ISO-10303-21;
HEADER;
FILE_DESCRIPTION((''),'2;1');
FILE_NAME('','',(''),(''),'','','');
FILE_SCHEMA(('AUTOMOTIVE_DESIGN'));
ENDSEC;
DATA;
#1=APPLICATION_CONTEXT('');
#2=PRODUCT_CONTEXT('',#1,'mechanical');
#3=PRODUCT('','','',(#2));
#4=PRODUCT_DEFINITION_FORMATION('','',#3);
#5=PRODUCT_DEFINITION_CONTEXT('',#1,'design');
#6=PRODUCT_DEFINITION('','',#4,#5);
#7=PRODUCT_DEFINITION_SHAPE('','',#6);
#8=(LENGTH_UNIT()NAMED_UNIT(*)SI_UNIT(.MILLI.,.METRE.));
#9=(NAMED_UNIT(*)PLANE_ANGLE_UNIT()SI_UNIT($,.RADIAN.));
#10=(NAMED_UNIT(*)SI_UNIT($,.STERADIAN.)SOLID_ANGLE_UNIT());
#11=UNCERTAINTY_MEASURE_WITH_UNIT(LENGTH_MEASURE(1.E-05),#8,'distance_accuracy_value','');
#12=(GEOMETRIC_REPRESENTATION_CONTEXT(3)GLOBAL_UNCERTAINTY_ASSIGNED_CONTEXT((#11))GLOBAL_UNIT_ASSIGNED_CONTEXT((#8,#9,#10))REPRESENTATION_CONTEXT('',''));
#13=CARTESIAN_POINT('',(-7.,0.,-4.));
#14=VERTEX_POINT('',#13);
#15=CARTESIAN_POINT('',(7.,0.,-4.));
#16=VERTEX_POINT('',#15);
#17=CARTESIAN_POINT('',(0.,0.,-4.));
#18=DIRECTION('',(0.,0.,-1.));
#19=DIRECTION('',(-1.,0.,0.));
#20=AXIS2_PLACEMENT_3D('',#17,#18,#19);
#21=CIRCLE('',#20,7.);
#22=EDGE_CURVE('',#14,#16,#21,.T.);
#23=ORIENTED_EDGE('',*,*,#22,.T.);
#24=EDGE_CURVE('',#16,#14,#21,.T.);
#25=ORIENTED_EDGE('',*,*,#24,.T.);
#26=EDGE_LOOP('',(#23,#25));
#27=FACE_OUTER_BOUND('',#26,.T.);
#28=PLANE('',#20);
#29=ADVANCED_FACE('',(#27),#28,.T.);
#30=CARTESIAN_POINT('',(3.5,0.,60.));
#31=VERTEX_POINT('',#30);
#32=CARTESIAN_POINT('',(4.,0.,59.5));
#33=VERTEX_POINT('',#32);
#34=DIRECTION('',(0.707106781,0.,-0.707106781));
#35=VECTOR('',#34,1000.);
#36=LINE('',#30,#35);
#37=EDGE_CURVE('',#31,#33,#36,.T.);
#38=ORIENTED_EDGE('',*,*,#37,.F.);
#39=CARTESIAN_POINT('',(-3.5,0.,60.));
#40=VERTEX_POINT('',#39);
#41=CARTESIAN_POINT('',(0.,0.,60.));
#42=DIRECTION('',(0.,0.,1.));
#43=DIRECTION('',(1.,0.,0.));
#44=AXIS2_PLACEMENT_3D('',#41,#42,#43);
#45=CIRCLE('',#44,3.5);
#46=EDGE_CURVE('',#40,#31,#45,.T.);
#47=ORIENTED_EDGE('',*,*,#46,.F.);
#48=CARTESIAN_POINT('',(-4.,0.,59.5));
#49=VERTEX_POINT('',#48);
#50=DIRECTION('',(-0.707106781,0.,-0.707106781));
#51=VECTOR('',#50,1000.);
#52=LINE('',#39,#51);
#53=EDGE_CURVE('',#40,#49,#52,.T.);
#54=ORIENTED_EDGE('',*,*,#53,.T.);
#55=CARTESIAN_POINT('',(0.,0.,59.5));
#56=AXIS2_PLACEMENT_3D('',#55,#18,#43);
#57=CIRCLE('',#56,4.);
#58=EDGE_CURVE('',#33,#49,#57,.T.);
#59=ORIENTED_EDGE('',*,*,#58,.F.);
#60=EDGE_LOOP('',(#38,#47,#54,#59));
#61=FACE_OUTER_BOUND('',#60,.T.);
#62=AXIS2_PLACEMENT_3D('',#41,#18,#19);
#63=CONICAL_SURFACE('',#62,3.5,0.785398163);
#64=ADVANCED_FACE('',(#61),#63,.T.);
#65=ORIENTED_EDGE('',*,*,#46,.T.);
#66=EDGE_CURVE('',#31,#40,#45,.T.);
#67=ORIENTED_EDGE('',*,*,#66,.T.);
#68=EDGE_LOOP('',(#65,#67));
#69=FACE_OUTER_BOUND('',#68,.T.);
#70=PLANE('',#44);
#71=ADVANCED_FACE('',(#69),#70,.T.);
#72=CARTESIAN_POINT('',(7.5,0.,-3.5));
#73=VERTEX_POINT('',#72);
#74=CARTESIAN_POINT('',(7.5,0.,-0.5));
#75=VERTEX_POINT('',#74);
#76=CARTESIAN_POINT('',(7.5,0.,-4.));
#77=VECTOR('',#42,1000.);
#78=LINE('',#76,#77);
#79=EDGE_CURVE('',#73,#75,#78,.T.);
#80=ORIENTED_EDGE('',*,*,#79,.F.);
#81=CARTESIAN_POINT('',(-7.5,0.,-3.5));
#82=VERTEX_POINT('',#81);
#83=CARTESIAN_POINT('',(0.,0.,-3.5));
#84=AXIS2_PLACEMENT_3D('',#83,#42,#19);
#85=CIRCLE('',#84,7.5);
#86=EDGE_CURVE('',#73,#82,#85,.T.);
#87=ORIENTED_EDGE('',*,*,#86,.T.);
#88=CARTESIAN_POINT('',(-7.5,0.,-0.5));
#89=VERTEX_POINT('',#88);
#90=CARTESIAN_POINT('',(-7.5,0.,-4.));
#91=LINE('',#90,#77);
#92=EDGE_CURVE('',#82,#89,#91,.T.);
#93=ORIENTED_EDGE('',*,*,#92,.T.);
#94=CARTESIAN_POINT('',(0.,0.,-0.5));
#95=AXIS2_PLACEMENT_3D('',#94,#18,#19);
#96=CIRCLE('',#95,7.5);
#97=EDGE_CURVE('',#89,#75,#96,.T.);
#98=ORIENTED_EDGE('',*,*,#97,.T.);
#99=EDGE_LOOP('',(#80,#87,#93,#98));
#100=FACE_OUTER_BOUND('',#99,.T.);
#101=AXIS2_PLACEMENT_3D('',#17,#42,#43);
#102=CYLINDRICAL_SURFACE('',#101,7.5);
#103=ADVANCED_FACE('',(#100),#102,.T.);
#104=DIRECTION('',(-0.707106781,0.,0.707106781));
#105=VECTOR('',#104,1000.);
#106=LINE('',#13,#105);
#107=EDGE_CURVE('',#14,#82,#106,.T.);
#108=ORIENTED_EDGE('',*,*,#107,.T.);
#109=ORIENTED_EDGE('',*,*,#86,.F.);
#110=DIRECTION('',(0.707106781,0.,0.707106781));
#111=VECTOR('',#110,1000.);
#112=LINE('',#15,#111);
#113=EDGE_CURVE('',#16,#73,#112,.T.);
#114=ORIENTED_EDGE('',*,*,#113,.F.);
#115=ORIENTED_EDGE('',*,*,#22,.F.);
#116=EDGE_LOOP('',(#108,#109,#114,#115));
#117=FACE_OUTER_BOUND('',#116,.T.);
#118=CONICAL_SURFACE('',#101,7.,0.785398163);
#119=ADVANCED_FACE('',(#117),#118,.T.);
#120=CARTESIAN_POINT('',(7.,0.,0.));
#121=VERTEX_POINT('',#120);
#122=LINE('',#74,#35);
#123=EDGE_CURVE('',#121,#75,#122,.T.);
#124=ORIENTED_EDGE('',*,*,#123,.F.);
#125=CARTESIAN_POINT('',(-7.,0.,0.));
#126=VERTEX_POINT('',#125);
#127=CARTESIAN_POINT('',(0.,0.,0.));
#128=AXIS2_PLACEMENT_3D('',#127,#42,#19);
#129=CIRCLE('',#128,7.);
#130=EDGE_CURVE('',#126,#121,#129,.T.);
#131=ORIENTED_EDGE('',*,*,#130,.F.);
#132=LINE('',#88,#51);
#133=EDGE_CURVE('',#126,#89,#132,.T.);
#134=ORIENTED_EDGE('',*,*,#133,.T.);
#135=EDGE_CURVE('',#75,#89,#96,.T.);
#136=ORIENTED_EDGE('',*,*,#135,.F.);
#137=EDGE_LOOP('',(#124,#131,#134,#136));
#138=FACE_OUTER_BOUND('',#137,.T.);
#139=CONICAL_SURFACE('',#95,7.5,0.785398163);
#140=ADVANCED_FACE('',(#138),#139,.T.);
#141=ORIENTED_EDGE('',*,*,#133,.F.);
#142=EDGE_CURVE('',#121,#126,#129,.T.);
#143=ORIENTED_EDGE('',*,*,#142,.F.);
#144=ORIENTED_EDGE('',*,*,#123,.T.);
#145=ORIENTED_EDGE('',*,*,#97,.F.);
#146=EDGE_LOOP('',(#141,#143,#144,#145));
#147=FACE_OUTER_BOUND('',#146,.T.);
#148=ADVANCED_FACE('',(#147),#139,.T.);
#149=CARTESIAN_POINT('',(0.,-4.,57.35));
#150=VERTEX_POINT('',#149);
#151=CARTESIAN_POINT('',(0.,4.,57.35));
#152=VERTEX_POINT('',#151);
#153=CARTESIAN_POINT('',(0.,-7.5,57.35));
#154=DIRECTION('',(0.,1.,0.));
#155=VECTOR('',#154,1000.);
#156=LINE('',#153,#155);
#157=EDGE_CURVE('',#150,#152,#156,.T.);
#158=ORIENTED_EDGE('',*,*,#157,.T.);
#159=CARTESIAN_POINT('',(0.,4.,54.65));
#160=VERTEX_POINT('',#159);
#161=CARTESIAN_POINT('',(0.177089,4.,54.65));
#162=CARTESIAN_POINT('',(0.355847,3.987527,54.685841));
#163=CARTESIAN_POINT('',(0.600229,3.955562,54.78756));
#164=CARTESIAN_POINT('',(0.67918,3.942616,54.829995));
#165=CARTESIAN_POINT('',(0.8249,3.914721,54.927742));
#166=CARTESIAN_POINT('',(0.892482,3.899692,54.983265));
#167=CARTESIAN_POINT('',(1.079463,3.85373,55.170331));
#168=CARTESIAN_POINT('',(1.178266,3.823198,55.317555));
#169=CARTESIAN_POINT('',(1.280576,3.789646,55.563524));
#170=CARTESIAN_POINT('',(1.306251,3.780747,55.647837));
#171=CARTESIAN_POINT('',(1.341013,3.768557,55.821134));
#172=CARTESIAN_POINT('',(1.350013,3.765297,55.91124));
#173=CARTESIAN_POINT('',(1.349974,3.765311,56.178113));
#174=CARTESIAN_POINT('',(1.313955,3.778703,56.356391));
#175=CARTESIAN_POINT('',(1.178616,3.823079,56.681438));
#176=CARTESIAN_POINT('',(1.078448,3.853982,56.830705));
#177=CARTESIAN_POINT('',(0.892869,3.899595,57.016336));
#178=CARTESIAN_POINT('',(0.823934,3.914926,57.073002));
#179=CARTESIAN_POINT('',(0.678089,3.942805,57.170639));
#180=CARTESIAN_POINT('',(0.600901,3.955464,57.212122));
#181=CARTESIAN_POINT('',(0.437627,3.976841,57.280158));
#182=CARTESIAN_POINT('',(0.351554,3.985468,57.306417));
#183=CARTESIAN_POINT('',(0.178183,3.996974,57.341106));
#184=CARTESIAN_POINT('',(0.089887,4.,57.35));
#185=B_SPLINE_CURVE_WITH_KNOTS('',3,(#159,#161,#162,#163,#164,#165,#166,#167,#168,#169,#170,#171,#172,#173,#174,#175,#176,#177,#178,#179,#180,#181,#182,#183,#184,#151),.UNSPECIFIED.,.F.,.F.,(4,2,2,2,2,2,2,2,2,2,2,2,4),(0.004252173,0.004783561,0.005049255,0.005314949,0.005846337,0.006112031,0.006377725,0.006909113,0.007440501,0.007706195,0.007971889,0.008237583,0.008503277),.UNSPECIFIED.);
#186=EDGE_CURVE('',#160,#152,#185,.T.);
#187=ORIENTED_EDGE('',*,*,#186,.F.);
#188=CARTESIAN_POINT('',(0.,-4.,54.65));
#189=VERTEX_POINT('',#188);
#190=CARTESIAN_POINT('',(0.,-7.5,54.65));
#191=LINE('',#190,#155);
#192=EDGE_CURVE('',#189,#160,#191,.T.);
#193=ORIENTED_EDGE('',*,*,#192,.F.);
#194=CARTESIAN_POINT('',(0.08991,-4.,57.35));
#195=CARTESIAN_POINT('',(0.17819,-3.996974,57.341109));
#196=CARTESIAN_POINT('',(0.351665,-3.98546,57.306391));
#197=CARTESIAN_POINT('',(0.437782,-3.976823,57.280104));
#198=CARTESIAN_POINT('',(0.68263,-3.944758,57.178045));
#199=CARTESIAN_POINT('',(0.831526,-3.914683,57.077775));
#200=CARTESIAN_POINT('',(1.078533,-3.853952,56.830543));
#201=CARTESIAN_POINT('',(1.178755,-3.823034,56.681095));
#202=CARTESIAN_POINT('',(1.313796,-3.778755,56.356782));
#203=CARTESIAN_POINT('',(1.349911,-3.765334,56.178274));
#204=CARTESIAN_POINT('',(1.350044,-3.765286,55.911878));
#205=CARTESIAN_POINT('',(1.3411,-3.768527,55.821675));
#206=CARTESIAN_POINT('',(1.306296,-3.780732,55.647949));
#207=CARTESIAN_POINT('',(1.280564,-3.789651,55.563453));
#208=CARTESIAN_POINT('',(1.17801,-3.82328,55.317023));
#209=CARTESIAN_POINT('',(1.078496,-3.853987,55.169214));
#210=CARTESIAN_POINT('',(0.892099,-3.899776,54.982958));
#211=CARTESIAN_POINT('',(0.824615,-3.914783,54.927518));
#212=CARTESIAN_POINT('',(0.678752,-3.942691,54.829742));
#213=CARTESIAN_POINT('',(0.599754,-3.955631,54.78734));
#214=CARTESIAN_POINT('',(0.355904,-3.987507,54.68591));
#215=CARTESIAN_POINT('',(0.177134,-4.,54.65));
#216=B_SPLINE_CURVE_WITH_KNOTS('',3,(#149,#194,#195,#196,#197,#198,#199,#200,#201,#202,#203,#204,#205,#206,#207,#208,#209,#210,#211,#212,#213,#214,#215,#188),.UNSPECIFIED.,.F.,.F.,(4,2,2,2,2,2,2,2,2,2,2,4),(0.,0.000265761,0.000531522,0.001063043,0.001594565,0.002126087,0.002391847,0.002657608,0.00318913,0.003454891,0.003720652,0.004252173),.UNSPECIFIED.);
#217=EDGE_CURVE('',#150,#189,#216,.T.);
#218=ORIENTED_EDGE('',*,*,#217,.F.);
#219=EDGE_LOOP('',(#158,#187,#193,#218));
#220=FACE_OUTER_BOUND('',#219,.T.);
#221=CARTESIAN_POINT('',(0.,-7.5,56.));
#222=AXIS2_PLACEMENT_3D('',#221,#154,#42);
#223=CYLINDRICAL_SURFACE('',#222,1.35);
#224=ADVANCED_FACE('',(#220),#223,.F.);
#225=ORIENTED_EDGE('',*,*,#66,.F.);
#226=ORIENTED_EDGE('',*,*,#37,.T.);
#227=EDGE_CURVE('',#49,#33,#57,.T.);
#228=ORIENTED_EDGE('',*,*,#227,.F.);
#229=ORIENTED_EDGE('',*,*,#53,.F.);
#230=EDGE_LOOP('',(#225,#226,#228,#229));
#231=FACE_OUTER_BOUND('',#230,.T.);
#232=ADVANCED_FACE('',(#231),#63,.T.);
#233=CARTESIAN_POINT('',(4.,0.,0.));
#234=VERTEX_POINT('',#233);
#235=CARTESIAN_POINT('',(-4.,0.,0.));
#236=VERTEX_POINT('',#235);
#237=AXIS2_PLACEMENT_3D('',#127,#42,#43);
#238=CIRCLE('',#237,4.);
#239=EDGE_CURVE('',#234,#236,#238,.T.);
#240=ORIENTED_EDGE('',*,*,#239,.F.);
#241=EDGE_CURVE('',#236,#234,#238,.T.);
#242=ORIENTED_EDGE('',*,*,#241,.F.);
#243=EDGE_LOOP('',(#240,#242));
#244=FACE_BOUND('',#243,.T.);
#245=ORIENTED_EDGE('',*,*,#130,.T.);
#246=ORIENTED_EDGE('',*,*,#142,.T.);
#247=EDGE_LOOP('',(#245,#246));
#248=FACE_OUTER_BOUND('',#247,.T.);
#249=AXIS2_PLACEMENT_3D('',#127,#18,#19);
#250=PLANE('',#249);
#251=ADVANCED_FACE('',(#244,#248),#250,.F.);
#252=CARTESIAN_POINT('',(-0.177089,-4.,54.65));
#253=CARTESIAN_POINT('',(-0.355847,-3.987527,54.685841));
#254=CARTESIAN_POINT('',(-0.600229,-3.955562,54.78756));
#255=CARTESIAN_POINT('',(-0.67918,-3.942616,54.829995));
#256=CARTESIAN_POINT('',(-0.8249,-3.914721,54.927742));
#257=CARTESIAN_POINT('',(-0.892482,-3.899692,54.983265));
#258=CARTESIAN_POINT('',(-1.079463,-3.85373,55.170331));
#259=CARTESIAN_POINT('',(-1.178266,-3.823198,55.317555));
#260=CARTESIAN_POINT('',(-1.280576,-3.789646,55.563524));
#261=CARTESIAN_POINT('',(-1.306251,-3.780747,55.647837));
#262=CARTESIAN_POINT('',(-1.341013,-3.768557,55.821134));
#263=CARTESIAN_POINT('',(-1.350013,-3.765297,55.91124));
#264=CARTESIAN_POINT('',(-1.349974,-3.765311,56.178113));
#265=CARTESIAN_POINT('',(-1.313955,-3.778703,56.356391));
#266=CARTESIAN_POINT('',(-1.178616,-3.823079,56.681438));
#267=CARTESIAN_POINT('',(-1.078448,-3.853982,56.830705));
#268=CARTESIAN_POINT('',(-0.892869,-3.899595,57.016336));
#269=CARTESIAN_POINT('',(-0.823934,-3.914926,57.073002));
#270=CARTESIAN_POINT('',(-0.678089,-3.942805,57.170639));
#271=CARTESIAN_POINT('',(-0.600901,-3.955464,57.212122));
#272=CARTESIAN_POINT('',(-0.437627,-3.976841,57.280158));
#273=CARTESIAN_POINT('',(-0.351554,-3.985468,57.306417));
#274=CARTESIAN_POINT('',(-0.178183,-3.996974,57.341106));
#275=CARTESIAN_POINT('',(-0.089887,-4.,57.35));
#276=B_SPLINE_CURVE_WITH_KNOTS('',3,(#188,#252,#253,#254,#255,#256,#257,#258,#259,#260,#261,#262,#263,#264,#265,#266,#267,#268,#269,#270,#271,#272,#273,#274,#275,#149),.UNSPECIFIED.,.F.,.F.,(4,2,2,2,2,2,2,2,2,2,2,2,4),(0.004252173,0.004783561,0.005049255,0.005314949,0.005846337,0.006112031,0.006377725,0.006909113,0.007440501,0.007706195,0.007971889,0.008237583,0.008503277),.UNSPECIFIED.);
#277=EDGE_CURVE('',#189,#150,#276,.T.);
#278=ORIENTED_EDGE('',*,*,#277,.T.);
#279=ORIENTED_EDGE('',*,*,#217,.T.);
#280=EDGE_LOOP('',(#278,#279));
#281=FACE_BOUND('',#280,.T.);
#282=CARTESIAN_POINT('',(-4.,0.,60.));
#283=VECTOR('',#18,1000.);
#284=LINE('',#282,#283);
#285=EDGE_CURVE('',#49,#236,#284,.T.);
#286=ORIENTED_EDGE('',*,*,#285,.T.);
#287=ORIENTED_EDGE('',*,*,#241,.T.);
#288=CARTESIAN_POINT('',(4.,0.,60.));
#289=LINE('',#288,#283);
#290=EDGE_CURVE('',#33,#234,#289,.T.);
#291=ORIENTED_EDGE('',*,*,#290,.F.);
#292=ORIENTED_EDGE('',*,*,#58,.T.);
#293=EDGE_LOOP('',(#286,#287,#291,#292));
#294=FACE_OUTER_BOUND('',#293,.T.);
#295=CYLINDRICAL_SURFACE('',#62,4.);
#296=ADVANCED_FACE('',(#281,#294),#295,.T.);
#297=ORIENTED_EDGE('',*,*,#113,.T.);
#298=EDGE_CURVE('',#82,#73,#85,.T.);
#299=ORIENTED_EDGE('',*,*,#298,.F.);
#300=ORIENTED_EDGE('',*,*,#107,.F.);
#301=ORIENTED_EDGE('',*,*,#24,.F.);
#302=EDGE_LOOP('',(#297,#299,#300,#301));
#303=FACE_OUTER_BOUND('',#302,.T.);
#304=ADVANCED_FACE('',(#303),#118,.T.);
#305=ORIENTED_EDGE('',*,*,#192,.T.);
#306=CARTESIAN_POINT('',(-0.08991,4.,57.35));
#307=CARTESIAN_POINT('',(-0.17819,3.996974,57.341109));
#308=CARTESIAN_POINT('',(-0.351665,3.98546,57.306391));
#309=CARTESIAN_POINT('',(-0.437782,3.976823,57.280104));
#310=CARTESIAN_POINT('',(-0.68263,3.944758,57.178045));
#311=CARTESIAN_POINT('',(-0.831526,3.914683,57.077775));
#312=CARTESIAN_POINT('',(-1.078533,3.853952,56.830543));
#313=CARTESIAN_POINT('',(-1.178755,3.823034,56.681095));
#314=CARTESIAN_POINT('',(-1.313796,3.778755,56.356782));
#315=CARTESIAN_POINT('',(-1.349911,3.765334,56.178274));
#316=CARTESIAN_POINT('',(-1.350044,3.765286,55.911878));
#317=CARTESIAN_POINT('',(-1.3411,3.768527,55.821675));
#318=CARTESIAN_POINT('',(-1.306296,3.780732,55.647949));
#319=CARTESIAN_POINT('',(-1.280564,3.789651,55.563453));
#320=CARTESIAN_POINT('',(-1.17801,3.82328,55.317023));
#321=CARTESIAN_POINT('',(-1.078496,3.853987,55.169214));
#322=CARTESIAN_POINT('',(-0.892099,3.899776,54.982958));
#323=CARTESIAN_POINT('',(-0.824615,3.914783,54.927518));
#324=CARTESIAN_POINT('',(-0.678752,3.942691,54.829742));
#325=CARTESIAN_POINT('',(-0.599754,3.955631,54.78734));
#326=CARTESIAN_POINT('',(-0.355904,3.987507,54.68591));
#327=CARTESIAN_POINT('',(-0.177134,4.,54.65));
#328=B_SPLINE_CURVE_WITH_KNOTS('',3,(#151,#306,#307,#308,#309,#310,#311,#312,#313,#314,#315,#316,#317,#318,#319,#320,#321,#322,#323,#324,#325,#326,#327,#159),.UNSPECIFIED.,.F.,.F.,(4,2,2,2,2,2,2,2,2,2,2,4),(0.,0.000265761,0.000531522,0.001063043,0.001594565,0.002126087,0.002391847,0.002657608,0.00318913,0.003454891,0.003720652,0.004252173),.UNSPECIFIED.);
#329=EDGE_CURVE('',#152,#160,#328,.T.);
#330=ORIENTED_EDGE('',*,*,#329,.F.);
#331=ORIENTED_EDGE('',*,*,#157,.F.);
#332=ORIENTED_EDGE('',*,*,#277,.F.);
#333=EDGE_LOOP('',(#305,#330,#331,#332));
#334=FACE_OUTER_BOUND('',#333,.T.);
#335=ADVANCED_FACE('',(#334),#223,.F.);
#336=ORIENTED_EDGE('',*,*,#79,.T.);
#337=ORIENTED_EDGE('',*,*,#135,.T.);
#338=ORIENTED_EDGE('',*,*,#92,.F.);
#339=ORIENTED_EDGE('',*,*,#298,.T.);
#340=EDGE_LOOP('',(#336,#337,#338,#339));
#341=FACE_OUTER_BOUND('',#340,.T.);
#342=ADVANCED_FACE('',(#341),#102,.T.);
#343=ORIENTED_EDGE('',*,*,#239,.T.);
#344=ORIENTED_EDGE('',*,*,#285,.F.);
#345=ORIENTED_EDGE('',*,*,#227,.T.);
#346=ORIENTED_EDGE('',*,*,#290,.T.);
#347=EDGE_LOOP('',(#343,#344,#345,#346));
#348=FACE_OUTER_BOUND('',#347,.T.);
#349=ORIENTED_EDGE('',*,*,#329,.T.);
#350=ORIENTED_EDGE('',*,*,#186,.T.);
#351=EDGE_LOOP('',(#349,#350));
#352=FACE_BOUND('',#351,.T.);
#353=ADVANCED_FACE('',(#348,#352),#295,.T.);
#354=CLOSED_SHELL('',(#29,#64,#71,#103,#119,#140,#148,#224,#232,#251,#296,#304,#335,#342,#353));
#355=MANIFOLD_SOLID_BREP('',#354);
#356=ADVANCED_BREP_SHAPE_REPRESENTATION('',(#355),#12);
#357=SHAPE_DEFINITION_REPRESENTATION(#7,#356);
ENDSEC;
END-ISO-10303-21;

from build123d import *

# Parameters (mm, degrees)
SKETCH1_R               = 4
BOSS_EXTRUDE1_DEPTH     = 60
SKETCH2_R               = 7.5
BOSS_EXTRUDE2_DEPTH     = 4
CUT_EXTRUDE1_DEPTH      = 61.930288035
CUT_EXTRUDE1_DEPTH_BACK = 61.930288035
SKETCH3_R               = 1.35
CHAMFER1_SIZE           = 0.5


with BuildPart() as part:
    # Sketch1 → Boss-Extrude1 (new body)
    with BuildSketch(Plane.XY):
        Circle(SKETCH1_R)
    extrude(amount=BOSS_EXTRUDE1_DEPTH)

    # Sketch2 → Boss-Extrude2 (add)
    with BuildSketch(Plane(origin=(0, 0, 0), x_dir=(-1, 0, 0), z_dir=(0, 0, -1))):
        Circle(SKETCH2_R)
    extrude(amount=BOSS_EXTRUDE2_DEPTH)

    # Sketch3 → Cut-Extrude1 (cut, two sides: drawn at the far end of the back side and taken through both)
    with BuildSketch(Plane(origin=(0, 0, 0), x_dir=(1, 0, 0), z_dir=(0, 1, 0)).offset(-CUT_EXTRUDE1_DEPTH_BACK)):
        with Locations(Location((0, -56, 0), (0, 0, 270))):
            Circle(SKETCH3_R)
    extrude(amount=CUT_EXTRUDE1_DEPTH + CUT_EXTRUDE1_DEPTH_BACK, mode=Mode.SUBTRACT)

    # Chamfer1
    chamfer1_edges = [part.edges().sort_by_distance(p)[0] for p in [
        (-4, 0, 60),
        (7.5, 0, 0),
        (7.5, 0, -4),
    ]]
    chamfer(chamfer1_edges, length=CHAMFER1_SIZE)


solid = part.part
